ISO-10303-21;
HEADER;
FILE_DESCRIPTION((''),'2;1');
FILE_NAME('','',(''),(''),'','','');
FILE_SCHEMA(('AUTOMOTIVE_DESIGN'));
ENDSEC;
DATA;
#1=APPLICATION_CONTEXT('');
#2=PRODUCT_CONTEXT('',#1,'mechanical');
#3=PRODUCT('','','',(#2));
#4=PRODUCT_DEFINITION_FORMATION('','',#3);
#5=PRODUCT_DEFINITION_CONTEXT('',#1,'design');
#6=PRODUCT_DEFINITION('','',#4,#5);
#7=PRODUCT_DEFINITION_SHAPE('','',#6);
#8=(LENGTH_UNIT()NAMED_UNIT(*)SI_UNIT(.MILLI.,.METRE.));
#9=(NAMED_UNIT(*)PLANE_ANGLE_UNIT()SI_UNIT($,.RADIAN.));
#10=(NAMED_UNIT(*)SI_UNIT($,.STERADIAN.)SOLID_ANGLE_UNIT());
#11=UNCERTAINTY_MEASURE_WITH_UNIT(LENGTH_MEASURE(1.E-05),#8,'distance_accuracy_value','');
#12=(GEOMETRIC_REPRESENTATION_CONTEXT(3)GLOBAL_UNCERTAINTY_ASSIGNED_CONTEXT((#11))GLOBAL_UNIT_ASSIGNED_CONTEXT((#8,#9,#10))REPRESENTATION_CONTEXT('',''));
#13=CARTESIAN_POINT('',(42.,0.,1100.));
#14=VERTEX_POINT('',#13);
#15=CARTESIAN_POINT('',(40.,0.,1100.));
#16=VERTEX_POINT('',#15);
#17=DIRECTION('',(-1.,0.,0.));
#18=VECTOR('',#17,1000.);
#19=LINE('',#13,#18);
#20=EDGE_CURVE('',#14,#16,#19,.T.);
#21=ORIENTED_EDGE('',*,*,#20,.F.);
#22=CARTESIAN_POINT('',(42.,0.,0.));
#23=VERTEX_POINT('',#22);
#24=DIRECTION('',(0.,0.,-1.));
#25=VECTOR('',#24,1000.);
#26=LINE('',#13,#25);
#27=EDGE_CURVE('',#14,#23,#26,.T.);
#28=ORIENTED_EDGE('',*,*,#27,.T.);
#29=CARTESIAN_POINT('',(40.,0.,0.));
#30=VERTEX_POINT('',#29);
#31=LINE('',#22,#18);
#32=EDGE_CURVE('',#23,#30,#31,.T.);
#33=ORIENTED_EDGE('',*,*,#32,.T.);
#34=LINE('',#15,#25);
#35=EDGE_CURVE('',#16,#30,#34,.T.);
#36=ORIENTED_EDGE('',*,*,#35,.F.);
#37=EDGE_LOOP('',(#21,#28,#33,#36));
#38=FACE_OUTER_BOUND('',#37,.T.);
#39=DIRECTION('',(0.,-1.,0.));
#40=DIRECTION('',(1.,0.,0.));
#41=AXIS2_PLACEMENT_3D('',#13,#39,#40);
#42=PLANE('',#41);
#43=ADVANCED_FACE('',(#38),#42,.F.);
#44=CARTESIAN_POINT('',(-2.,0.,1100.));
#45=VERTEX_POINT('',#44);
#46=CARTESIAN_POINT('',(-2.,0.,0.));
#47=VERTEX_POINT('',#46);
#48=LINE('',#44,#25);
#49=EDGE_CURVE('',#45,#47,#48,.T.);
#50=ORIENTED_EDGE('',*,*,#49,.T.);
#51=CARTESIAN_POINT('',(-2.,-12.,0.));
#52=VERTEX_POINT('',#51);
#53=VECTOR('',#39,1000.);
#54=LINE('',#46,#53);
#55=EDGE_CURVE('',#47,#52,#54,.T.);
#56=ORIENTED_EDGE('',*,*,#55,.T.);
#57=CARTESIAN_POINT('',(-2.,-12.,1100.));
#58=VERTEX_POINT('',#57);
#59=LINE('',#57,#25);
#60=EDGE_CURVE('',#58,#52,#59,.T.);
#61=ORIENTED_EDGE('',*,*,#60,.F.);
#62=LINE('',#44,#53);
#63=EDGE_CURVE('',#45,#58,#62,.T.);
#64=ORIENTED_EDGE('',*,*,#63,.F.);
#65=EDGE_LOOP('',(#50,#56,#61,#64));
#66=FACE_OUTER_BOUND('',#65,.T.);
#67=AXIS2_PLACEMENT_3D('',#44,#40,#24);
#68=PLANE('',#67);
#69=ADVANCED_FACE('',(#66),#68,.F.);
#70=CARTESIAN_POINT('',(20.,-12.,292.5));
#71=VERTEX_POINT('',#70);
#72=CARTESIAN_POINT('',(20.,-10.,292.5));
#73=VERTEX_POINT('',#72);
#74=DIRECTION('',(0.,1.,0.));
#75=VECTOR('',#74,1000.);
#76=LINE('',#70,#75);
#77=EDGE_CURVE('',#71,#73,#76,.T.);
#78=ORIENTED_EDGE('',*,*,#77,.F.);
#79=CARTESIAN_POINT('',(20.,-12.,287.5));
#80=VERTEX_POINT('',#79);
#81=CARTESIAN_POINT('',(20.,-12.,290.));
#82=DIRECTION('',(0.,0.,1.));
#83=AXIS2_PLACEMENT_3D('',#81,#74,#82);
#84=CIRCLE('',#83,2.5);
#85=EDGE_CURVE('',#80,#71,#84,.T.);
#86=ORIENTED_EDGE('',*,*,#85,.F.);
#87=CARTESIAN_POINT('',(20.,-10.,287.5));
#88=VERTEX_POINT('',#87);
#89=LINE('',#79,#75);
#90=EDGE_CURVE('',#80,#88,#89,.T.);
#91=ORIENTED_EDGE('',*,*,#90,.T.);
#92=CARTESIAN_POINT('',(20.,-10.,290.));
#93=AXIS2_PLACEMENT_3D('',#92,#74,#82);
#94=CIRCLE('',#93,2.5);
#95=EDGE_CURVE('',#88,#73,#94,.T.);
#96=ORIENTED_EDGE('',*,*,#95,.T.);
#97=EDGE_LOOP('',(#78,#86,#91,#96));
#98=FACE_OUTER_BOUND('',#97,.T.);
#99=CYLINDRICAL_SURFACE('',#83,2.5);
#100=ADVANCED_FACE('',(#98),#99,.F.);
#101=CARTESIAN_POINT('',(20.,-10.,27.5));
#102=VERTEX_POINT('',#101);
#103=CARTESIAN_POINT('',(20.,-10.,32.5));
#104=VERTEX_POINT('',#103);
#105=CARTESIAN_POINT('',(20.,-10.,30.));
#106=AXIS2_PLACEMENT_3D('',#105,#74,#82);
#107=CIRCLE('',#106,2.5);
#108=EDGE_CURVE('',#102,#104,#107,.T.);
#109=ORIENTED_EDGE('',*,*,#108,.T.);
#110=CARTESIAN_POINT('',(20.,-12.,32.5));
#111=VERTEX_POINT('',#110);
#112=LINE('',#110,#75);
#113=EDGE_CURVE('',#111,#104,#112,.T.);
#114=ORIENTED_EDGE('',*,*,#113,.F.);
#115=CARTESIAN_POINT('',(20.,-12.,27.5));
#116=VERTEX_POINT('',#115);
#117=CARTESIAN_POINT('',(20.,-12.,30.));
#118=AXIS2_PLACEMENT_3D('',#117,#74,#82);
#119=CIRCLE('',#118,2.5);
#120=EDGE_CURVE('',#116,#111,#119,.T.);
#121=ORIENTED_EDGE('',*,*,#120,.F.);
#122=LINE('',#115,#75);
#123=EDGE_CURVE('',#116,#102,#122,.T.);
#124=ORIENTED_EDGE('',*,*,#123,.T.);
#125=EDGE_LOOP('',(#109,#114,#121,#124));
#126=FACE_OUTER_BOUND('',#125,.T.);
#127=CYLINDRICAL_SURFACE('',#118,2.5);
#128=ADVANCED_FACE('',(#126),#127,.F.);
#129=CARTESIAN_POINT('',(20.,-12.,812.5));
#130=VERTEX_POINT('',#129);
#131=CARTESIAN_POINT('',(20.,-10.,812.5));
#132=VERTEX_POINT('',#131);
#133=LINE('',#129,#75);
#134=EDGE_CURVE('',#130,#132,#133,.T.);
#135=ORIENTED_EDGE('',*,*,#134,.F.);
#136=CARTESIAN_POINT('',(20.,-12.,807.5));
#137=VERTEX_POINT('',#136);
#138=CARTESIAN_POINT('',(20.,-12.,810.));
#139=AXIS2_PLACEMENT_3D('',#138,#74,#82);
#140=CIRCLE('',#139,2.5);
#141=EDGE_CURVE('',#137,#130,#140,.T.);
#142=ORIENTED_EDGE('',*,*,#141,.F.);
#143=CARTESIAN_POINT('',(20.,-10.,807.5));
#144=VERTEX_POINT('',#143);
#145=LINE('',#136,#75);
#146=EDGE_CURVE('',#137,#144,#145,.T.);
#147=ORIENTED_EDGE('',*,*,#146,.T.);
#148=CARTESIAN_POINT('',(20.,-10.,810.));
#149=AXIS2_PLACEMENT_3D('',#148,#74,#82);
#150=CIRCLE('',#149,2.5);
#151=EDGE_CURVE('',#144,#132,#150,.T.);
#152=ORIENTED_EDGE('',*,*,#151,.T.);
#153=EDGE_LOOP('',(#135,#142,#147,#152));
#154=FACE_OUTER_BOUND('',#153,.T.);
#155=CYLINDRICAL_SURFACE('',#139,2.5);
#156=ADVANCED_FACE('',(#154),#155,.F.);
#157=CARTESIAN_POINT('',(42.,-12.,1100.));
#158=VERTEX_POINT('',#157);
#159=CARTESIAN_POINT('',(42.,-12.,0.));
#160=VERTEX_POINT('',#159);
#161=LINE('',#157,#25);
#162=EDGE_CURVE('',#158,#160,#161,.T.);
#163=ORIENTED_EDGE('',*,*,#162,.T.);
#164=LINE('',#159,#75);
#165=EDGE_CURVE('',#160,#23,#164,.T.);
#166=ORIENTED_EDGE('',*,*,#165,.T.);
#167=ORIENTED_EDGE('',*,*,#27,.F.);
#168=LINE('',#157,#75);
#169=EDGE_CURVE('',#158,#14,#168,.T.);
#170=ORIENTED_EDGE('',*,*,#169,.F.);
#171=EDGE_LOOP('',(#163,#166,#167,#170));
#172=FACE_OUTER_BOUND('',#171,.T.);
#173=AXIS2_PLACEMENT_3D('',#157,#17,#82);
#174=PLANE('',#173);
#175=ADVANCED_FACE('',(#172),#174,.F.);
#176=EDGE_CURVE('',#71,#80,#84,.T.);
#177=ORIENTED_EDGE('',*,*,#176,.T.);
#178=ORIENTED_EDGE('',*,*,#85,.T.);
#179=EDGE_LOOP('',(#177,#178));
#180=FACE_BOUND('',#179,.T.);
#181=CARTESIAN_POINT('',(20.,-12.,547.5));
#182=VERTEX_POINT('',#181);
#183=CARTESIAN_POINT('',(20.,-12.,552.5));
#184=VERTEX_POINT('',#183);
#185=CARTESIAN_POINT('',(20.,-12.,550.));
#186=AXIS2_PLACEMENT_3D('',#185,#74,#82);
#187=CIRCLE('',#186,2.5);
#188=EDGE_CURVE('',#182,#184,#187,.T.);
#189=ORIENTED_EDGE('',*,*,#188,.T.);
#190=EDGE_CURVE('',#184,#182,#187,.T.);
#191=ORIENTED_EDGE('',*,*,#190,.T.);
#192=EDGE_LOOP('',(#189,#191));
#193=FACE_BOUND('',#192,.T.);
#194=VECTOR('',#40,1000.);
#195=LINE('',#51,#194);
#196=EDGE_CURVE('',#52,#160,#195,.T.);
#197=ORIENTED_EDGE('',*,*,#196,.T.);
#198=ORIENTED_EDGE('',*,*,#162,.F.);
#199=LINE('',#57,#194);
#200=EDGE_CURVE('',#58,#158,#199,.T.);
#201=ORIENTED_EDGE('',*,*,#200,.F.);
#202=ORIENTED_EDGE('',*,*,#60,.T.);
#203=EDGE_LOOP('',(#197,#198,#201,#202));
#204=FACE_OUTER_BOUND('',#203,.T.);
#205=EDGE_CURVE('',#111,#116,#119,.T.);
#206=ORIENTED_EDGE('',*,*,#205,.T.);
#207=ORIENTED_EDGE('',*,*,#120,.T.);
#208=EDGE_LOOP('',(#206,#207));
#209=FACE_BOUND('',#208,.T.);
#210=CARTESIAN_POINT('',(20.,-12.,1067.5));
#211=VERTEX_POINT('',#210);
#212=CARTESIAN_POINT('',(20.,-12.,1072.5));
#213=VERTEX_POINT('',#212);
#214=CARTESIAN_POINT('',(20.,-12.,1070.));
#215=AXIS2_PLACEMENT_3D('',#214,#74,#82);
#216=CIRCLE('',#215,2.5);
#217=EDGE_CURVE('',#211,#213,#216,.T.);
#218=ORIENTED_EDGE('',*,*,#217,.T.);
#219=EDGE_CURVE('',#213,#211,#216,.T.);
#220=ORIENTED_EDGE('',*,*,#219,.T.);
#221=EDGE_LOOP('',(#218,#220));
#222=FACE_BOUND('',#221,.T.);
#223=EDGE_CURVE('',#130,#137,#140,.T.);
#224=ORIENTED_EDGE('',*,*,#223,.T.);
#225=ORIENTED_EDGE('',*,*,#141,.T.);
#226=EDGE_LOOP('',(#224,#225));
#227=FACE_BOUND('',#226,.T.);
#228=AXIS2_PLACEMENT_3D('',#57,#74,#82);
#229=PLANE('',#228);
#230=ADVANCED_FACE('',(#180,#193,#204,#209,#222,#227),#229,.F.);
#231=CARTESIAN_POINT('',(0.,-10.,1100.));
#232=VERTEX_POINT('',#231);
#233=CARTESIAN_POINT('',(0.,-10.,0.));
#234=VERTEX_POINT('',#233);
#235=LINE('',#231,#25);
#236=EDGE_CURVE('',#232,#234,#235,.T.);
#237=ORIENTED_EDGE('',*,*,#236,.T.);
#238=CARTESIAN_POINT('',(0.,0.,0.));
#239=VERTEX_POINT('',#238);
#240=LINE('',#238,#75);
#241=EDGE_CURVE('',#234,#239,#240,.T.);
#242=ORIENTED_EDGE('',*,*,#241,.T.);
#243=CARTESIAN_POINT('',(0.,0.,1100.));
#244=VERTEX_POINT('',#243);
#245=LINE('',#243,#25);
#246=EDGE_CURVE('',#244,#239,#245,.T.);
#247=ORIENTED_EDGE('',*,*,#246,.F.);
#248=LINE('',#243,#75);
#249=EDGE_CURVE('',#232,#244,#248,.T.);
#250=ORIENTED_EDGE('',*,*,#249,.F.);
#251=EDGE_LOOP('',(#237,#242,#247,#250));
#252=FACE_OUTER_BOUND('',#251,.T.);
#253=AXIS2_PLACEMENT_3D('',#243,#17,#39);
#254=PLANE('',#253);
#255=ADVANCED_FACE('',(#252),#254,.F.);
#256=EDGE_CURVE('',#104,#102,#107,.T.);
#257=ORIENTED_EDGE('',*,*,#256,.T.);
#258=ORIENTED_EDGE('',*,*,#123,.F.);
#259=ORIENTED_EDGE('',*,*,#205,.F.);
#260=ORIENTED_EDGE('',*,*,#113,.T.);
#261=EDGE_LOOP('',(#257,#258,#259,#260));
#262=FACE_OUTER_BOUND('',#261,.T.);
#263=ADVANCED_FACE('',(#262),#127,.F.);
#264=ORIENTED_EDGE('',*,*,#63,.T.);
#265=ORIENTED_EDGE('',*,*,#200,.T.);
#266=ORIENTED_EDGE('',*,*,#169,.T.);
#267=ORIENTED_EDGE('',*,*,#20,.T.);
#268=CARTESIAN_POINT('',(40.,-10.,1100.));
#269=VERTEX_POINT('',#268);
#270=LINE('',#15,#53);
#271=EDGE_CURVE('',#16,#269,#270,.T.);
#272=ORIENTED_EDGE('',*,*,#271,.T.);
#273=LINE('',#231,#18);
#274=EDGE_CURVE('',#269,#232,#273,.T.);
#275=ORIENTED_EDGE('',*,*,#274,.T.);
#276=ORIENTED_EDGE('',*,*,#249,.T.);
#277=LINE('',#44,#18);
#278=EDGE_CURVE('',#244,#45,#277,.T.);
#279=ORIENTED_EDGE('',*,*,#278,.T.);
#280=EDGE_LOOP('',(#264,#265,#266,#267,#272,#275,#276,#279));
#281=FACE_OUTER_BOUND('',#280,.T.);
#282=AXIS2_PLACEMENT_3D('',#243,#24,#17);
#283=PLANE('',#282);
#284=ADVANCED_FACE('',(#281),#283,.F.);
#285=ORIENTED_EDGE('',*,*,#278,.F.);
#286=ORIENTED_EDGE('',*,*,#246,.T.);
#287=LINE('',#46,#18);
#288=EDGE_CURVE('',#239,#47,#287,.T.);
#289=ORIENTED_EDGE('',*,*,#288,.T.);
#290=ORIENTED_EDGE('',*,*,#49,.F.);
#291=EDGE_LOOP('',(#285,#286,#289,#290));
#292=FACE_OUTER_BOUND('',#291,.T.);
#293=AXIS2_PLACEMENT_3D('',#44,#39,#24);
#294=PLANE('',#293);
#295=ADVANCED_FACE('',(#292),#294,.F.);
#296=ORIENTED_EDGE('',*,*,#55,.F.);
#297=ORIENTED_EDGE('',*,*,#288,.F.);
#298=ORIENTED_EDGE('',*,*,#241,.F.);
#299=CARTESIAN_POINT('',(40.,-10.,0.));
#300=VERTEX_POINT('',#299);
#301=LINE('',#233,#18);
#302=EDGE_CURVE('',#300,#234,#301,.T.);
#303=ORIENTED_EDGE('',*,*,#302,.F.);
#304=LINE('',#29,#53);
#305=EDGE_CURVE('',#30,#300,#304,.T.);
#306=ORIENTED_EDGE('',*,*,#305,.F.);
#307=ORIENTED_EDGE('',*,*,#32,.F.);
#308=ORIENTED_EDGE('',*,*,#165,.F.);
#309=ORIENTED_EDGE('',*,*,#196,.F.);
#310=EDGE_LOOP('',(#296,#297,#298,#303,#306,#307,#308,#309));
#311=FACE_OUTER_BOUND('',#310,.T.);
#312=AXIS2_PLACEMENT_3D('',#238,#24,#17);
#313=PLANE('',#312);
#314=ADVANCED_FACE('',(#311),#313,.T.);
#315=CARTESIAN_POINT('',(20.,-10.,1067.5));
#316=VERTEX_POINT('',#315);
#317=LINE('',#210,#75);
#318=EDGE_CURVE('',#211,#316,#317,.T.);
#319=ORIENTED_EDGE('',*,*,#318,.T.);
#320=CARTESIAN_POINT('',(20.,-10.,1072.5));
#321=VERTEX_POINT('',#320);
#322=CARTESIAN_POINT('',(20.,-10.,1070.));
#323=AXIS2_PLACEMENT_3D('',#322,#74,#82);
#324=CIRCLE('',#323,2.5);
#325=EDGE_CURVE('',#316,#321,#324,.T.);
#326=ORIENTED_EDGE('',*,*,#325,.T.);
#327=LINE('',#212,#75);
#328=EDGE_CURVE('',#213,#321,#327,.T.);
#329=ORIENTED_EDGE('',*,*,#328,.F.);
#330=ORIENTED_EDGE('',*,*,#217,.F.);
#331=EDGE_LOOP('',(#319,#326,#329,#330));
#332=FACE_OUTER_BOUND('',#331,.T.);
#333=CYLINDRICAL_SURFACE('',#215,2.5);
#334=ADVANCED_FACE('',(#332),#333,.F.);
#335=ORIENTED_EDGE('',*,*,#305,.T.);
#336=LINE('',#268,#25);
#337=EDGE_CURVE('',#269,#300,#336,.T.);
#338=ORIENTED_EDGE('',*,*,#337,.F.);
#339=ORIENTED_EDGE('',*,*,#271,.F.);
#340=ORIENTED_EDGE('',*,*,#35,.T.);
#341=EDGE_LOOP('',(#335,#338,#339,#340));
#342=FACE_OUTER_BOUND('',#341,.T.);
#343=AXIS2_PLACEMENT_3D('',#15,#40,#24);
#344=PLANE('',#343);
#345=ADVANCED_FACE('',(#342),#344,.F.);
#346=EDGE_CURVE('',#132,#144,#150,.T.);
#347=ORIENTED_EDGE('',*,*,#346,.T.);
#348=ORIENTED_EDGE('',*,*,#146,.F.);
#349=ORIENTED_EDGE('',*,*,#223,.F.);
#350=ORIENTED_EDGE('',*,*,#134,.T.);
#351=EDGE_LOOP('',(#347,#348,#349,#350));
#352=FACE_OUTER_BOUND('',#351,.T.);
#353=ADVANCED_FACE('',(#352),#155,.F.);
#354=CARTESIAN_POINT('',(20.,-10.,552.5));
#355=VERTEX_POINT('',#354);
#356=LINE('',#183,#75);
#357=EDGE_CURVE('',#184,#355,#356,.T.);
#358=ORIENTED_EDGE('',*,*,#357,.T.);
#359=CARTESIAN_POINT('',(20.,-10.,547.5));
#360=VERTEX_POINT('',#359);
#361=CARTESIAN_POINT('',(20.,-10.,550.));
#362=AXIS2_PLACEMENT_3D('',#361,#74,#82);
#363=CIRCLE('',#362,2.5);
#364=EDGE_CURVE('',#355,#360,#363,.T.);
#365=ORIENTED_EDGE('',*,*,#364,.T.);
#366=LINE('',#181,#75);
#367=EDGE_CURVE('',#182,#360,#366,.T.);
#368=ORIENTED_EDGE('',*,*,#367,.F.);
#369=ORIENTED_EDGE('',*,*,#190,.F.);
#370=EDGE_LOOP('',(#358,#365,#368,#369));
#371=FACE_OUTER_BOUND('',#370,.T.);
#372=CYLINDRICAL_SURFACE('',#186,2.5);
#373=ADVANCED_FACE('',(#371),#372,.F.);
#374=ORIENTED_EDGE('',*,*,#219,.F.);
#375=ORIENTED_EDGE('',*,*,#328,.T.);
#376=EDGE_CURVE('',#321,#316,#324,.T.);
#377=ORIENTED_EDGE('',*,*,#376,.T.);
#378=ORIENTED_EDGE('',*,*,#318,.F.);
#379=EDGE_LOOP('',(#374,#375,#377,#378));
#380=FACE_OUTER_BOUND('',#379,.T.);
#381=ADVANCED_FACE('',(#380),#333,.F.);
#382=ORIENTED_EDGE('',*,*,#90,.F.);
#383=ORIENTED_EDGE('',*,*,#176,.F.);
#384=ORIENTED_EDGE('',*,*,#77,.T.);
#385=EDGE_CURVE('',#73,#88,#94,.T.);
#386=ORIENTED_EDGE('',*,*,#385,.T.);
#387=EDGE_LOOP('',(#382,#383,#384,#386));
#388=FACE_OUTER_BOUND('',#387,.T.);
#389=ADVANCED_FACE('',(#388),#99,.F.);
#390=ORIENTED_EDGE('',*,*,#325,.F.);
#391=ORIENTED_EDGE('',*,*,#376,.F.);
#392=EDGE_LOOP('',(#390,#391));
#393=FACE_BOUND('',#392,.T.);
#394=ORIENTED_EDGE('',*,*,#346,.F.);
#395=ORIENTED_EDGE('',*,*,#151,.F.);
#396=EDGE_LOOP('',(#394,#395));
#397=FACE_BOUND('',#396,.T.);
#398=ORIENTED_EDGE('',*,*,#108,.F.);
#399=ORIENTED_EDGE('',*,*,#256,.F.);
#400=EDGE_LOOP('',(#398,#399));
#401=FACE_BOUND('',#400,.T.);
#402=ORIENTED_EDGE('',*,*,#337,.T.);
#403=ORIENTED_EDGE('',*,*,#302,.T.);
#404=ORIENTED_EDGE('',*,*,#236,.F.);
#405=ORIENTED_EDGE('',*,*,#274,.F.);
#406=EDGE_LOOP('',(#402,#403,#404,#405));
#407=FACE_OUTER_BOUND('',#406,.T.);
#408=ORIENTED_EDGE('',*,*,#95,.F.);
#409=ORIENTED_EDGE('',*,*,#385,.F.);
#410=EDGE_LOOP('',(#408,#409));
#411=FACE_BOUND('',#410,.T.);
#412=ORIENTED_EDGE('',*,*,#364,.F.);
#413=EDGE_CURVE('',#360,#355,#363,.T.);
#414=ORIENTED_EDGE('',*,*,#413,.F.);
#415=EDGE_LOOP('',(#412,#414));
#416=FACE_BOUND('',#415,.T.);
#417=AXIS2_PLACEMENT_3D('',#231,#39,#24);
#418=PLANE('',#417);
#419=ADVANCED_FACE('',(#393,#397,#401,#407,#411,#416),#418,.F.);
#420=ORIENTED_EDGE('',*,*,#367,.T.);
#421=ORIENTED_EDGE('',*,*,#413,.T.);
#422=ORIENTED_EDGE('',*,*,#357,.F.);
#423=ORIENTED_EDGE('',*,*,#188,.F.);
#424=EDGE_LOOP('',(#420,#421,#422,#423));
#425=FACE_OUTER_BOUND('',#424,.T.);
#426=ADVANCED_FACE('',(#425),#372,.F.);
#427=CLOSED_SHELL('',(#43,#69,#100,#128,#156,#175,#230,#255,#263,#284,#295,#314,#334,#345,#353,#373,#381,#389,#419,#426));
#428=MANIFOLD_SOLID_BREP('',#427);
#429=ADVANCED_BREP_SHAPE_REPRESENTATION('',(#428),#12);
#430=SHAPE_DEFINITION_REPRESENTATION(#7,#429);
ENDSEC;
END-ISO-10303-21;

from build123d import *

# Parameters (mm, degrees)
EXTRUDE_1_DEPTH        = 1100
SKETCH_2_R             = 2.5
CUT_EXTRUDE_1_DEPTH    = 1101.846946673
PATTERN_LINEAR_1_COUNT = 5
PATTERN_LINEAR_1_PITCH = 260


with BuildPart() as part:
    # 草图1 → 凸台-拉伸1 (new body)
    with BuildSketch(Plane.XY):
        Polygon((0, 0), (0, -10), (40, -10), (40, 0), (42, 0), (42, -12), (-2, -12), (-2, 0), align=None)
    extrude(amount=EXTRUDE_1_DEPTH)

    # 草图2 → 切除-拉伸1 (cut, through all)
    with BuildSketch(Plane(origin=(0, -10, 0), x_dir=(1, 0, 0), z_dir=(0, 1, 0))):
        with Locations(Location((20, -30, 0), (0, 0, 270))):
            Circle(SKETCH_2_R)
    cut_extrude_1 = extrude(amount=-CUT_EXTRUDE_1_DEPTH, mode=Mode.SUBTRACT)

    # 阵列(线性)1: 切除-拉伸1 ×5
    with Locations(*[(0, 0, i * PATTERN_LINEAR_1_PITCH) for i in range(1, PATTERN_LINEAR_1_COUNT)]):
        add(cut_extrude_1, mode=Mode.SUBTRACT)


solid = part.part
